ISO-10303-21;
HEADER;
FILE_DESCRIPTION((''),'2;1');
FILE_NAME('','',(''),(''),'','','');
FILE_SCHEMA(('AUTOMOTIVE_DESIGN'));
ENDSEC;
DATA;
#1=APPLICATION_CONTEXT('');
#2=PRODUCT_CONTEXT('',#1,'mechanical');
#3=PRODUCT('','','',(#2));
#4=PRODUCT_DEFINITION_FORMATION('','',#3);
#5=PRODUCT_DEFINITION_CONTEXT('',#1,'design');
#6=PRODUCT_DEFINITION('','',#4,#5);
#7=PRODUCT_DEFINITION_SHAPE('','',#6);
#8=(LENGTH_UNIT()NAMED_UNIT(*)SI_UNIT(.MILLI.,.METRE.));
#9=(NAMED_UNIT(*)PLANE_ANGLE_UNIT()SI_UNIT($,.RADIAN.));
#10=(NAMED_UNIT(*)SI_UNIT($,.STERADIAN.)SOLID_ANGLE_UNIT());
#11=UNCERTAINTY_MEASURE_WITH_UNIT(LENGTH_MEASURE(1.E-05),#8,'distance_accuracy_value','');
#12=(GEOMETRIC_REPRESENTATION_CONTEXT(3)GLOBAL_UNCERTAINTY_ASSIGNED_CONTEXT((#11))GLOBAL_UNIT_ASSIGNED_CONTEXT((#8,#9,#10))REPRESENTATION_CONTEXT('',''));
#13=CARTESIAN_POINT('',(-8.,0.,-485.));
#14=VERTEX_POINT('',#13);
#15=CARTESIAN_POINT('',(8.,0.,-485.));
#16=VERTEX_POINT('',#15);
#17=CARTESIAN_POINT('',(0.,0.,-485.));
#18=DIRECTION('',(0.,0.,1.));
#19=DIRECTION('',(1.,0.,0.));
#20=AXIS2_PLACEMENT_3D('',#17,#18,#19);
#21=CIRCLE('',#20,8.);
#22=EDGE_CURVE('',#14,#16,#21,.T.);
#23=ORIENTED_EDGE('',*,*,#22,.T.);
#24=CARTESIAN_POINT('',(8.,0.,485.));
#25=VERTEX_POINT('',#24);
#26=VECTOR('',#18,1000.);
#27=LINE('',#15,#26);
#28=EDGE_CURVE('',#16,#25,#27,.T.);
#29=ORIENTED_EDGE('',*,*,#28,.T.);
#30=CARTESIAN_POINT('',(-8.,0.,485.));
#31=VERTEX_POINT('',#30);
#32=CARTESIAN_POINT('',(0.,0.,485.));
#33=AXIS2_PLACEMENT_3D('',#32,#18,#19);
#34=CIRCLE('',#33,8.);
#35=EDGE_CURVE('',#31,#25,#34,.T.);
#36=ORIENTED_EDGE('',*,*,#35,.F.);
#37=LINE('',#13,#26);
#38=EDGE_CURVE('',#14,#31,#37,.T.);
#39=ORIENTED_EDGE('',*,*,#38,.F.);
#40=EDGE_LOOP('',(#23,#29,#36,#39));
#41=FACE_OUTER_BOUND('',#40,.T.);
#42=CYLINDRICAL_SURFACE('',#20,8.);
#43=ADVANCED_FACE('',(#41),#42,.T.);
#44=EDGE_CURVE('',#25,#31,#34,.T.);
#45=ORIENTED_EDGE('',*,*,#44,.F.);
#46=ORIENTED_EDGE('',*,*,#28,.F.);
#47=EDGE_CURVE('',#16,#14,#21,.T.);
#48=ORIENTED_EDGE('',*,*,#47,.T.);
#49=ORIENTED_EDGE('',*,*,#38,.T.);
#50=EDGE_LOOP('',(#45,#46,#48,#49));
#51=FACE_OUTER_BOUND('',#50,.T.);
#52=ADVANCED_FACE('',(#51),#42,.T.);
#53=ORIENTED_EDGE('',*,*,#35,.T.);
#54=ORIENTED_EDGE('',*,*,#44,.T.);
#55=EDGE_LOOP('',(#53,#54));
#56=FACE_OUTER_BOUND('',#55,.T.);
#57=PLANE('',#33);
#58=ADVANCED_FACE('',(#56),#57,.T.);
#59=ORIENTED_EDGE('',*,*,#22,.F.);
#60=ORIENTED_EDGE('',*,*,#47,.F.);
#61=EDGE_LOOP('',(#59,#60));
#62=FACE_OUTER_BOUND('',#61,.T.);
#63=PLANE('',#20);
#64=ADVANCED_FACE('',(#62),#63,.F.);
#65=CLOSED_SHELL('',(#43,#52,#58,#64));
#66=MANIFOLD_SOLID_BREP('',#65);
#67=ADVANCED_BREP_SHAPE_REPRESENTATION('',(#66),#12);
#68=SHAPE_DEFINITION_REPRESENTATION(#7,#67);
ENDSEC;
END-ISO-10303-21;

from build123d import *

# Parameters (mm, degrees)
SKETCH_1_R      = 8
EXTRUDE_1_DEPTH = 485


with BuildPart() as part:
    # 草图1 → 凸台-拉伸1 (new, symmetric)
    with BuildSketch(Plane.XY):
        Circle(SKETCH_1_R)
    extrude(amount=EXTRUDE_1_DEPTH, both=True)


solid = part.part
